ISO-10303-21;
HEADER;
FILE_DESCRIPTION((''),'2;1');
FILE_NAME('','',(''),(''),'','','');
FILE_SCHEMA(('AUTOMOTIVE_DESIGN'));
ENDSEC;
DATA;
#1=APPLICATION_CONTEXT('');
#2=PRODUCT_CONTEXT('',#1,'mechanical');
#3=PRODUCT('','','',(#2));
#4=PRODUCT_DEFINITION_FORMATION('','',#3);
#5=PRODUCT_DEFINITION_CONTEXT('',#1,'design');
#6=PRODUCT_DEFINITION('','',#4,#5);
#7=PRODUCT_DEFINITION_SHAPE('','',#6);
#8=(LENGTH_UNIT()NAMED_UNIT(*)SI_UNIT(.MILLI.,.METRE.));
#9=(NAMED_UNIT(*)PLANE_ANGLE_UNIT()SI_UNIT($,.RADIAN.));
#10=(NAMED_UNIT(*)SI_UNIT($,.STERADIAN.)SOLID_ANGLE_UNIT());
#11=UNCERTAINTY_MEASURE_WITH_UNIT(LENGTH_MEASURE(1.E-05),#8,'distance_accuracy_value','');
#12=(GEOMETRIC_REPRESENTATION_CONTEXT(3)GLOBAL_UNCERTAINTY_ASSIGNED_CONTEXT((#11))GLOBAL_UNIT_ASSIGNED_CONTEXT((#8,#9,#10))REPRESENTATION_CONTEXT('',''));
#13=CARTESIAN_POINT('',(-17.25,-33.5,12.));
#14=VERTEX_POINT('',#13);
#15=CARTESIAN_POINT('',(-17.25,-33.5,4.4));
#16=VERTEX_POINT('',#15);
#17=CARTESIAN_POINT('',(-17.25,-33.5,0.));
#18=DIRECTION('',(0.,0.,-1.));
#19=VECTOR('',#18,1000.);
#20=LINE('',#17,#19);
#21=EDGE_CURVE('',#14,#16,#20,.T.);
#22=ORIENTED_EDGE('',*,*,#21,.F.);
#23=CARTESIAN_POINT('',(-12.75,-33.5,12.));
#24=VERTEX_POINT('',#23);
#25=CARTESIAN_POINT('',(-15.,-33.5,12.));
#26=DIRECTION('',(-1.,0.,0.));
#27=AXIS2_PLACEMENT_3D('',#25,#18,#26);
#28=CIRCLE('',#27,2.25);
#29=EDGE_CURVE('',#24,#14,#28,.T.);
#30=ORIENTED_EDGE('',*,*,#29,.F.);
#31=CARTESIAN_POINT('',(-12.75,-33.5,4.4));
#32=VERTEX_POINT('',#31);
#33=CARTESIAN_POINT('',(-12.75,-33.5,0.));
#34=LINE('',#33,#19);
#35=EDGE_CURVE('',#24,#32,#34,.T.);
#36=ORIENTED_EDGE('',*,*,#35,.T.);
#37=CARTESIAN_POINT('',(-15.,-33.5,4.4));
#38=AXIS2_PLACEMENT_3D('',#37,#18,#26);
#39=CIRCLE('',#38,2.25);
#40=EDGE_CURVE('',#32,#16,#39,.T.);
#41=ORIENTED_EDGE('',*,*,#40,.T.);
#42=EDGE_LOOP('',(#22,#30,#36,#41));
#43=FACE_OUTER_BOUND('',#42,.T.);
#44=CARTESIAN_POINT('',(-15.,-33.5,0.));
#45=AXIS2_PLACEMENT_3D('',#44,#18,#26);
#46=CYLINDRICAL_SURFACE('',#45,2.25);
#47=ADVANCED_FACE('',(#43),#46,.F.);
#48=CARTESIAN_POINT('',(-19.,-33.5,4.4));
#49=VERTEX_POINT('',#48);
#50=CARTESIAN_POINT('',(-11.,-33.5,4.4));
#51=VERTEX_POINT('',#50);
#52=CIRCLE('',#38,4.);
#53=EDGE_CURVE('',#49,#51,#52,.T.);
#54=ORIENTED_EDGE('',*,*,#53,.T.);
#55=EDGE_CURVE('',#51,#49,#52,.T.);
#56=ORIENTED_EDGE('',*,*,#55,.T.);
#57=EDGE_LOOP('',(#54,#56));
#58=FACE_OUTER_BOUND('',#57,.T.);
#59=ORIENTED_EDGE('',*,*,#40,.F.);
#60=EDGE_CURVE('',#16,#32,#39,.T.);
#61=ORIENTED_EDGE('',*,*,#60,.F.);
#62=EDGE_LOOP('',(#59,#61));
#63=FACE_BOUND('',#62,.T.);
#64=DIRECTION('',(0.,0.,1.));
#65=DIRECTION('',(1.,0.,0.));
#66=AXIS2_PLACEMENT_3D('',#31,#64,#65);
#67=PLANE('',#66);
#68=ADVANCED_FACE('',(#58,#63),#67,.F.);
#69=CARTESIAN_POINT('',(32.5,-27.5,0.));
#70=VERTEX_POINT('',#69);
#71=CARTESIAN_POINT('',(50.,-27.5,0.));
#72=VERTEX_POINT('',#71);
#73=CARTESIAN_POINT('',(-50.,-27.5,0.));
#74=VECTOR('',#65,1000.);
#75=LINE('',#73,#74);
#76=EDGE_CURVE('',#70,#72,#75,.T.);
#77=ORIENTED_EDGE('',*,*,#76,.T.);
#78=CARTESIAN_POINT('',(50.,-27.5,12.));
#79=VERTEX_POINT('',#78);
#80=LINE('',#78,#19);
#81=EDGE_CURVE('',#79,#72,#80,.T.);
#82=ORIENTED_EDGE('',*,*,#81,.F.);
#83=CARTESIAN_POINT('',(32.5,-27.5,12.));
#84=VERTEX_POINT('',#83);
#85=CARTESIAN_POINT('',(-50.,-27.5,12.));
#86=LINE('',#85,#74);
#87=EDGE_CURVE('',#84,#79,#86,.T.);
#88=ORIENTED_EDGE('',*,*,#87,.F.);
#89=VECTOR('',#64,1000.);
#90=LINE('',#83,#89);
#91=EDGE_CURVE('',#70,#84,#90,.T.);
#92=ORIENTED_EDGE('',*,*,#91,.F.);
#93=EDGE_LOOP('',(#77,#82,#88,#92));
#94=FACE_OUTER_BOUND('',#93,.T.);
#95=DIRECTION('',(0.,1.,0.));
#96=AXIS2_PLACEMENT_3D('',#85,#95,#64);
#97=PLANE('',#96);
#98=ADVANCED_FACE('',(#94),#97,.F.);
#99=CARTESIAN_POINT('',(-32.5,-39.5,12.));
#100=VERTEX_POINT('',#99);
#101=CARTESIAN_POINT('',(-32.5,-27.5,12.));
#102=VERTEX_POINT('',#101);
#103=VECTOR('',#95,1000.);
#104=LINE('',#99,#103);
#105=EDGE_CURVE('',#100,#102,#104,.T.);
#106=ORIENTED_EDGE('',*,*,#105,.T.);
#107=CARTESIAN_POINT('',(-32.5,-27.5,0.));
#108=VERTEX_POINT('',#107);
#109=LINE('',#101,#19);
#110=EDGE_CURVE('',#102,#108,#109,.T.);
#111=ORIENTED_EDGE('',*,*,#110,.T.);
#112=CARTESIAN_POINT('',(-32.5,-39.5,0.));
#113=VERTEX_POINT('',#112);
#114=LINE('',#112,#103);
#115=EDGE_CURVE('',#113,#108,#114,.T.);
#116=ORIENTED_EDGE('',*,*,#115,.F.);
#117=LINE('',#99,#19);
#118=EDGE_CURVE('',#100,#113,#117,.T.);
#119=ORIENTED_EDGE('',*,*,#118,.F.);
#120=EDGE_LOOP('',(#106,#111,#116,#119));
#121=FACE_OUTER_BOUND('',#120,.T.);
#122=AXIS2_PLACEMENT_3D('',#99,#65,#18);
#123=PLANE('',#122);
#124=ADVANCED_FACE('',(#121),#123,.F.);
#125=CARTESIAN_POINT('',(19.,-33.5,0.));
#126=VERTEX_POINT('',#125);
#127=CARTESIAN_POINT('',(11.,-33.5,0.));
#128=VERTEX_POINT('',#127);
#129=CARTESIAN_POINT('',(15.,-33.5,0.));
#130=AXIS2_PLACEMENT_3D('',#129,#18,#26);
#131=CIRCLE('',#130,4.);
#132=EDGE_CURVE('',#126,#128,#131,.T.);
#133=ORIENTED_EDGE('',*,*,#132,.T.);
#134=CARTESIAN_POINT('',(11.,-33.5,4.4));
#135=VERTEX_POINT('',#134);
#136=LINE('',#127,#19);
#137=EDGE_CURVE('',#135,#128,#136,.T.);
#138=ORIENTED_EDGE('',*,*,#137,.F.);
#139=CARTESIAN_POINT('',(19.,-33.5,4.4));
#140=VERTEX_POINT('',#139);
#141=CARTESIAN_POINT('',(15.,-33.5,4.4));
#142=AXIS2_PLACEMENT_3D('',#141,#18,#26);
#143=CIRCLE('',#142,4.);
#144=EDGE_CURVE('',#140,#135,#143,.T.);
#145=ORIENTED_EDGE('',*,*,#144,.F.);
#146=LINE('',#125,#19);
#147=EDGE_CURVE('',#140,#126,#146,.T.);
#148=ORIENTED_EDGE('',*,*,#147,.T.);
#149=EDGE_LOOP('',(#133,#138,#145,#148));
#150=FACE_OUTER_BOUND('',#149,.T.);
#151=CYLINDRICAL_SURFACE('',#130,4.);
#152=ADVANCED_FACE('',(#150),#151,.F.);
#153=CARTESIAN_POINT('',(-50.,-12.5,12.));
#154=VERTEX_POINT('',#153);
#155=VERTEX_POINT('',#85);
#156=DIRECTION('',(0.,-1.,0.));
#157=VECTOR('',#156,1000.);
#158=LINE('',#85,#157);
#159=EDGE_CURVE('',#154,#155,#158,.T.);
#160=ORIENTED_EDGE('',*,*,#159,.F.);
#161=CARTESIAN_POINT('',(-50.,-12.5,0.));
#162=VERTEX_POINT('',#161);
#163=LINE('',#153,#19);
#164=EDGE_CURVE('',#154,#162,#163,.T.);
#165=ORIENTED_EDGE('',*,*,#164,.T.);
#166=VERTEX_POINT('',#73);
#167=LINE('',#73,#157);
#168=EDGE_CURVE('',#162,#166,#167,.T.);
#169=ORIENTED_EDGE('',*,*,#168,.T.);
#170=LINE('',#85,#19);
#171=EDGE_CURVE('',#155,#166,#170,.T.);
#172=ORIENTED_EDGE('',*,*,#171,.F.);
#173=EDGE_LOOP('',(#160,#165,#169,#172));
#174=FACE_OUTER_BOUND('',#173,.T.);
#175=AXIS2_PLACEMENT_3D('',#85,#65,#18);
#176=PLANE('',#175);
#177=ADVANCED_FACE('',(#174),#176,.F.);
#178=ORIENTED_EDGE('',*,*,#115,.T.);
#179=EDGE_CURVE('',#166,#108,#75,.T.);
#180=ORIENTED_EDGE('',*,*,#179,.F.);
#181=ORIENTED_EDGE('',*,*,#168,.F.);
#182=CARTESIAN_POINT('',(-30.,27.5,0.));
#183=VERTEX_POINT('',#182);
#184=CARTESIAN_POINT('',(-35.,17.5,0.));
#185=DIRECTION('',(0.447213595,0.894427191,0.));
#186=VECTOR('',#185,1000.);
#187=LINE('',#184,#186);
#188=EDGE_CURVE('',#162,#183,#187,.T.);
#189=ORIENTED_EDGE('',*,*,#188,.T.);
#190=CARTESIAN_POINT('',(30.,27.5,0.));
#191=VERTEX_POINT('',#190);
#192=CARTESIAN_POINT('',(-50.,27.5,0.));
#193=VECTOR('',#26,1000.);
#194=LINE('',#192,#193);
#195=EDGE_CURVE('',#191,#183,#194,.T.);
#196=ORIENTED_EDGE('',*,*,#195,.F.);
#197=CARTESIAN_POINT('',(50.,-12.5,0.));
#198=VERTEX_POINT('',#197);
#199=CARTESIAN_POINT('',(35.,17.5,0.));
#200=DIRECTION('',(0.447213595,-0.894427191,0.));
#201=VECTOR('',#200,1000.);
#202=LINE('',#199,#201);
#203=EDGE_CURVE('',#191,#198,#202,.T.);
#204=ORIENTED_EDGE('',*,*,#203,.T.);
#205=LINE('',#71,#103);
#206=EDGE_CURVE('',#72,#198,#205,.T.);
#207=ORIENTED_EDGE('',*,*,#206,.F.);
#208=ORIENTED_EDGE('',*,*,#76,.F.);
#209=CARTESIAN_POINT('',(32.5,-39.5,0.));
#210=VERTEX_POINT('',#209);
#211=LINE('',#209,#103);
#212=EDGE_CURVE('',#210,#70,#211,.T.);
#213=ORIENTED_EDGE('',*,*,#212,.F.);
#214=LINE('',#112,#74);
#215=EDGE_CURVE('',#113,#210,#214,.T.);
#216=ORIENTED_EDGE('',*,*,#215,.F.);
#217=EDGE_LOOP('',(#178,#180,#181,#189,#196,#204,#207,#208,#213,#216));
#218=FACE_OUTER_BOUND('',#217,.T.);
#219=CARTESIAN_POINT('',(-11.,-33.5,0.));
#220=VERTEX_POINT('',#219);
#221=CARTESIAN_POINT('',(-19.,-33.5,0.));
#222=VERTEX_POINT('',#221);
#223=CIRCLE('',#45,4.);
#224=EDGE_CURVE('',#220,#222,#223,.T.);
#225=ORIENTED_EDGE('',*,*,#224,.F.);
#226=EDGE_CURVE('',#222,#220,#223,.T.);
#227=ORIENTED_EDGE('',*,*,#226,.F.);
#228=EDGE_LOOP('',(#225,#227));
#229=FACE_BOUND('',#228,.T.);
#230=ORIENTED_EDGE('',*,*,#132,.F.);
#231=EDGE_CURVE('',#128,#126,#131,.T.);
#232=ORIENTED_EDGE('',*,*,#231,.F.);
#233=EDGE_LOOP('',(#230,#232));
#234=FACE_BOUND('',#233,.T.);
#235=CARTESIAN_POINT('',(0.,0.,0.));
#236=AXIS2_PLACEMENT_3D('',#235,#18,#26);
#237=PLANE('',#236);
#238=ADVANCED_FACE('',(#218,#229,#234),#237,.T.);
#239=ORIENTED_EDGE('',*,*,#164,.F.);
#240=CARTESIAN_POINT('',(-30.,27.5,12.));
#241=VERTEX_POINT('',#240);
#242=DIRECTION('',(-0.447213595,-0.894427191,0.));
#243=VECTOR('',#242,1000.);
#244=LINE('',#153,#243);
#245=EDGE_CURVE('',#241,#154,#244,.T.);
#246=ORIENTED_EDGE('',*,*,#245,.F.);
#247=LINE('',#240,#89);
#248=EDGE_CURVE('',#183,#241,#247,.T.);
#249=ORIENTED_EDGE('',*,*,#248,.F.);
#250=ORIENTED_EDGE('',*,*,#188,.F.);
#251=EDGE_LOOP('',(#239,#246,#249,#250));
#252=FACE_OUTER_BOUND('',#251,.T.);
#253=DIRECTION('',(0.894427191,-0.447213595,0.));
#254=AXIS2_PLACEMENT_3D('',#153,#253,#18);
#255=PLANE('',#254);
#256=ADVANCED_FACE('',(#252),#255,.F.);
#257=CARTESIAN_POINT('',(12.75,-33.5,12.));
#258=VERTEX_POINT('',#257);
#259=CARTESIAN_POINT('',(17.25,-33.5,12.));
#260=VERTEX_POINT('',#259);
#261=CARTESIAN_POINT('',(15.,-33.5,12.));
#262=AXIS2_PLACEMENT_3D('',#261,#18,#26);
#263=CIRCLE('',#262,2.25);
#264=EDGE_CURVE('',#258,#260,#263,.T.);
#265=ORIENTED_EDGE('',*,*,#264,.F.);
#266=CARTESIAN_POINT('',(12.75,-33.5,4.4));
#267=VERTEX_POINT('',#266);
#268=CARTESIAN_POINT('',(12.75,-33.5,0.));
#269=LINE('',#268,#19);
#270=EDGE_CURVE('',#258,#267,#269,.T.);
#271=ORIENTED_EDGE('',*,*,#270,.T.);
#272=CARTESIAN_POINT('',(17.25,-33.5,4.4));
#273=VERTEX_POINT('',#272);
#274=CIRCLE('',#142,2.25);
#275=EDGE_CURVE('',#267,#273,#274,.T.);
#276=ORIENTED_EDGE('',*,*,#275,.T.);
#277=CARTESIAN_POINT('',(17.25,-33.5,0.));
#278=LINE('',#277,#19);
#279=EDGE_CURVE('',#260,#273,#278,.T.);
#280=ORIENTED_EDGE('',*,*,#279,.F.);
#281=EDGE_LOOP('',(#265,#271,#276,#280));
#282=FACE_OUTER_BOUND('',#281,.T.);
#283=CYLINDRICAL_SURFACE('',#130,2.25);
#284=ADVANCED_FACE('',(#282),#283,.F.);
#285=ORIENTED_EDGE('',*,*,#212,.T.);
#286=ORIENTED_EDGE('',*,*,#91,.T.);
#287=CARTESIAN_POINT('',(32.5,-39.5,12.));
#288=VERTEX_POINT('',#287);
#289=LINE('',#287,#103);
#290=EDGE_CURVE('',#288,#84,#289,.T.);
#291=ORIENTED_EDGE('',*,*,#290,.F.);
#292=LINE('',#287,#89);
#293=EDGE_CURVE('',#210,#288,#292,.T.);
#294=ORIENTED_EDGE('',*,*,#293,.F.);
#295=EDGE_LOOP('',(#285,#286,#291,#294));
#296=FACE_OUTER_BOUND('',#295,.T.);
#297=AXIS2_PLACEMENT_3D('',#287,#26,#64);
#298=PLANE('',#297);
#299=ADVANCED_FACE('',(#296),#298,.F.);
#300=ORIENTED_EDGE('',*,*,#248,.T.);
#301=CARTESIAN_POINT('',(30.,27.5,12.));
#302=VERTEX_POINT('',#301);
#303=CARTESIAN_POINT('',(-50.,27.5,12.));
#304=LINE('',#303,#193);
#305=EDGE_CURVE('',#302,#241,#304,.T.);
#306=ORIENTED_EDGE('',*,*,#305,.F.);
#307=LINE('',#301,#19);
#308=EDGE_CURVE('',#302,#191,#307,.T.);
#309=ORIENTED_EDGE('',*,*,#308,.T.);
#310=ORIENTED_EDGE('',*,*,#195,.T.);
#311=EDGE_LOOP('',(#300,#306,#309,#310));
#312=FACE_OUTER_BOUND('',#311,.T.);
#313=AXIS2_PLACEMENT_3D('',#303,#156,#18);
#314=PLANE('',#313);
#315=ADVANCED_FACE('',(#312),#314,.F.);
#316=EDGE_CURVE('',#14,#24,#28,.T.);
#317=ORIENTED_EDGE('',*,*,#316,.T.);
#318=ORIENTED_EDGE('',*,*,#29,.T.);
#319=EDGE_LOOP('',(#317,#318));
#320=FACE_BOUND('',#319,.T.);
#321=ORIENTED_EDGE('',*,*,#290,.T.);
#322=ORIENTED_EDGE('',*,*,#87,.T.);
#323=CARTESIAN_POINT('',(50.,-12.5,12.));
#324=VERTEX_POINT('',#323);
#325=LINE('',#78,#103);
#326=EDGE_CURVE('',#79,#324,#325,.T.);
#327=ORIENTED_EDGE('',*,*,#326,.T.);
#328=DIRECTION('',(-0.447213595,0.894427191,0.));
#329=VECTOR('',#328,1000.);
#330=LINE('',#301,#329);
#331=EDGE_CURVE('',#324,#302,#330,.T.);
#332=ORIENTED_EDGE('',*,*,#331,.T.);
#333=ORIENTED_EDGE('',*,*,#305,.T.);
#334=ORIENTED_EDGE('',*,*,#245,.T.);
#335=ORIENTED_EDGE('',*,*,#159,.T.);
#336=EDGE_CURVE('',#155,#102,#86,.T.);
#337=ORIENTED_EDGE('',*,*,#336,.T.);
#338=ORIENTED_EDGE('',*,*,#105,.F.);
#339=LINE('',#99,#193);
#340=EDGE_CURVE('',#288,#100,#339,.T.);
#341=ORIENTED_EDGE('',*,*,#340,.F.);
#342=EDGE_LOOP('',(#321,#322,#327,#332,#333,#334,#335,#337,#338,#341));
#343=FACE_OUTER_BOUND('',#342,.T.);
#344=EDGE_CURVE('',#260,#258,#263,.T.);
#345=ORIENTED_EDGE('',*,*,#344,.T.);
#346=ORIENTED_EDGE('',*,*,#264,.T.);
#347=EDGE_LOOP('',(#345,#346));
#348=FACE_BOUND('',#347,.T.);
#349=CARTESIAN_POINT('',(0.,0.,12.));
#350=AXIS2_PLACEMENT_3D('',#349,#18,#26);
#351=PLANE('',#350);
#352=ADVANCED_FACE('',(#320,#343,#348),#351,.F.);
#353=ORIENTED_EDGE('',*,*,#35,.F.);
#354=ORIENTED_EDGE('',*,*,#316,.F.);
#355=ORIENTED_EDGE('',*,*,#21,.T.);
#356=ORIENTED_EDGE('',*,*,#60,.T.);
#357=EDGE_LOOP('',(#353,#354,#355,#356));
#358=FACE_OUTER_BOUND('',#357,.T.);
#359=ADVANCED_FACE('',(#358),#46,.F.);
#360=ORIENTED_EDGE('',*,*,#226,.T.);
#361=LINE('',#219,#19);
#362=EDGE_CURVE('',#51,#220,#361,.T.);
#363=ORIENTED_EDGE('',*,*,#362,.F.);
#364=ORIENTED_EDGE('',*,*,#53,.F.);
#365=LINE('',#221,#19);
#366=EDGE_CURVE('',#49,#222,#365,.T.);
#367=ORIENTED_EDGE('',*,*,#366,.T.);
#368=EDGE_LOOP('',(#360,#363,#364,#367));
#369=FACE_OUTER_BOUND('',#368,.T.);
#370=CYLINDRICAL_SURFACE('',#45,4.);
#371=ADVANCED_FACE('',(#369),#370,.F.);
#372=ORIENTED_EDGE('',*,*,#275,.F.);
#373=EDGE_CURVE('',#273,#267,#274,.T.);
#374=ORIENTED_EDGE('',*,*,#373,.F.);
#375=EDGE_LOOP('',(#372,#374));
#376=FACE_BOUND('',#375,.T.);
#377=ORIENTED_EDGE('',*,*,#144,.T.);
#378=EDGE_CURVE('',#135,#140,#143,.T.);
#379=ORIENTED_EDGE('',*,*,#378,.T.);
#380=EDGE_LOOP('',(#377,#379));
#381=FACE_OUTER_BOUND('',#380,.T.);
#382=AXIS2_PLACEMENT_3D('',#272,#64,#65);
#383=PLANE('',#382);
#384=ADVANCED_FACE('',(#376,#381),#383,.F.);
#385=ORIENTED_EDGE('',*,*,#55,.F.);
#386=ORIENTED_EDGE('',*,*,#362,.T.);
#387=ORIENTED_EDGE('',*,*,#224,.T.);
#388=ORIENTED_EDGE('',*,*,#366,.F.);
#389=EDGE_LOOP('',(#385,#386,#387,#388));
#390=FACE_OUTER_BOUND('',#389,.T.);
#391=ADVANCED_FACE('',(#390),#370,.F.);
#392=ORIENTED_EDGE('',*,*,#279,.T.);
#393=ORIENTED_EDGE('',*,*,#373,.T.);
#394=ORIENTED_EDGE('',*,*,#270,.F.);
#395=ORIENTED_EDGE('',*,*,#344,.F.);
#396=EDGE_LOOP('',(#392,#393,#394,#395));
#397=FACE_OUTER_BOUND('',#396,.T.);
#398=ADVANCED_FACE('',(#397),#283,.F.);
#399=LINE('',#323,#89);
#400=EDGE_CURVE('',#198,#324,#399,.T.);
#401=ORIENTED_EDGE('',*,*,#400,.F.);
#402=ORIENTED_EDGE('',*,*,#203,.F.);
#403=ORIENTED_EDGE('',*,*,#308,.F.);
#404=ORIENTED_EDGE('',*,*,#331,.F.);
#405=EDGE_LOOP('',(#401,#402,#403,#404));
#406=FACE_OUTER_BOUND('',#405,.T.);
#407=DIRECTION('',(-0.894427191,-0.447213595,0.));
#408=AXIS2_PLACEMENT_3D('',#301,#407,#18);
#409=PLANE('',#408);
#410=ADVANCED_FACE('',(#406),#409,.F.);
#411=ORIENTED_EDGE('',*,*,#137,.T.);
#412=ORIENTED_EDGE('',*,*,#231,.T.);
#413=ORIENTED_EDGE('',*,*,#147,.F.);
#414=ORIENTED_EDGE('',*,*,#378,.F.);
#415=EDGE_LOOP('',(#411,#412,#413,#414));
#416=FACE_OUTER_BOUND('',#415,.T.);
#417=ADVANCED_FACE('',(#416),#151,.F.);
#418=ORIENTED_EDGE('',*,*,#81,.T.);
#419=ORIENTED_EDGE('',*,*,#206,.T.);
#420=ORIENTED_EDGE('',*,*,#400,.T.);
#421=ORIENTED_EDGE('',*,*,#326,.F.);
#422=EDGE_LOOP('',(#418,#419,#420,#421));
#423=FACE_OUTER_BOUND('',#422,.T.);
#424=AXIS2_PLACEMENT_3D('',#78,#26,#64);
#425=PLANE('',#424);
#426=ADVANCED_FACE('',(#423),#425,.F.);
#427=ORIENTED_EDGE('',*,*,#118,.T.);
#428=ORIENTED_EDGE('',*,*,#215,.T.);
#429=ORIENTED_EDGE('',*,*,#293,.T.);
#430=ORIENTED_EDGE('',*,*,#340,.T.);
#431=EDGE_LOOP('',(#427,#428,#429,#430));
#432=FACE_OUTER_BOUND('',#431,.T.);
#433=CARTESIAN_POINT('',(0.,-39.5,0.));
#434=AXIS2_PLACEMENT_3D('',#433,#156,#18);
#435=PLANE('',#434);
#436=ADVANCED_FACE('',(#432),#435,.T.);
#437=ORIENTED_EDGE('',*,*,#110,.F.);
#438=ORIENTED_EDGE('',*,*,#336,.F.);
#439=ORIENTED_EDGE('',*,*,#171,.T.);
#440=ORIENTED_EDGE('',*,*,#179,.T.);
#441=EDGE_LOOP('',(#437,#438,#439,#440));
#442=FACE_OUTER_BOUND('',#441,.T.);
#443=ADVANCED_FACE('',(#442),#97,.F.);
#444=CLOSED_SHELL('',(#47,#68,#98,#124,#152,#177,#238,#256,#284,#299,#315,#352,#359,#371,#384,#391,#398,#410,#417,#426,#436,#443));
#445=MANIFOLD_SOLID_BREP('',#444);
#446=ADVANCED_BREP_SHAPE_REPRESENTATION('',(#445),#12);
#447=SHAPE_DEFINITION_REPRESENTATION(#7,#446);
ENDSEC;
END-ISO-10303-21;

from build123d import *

# Parameters (mm, degrees)
SKETCH1_W                                           = 100
SKETCH1_H                                           = 55
BOSS_EXTRUDE1_DEPTH                                 = 12
SKETCH2_W                                           = 65
SKETCH2_H                                           = 12
BOSS_EXTRUDE2_DEPTH                                 = 12
CBORE_FOR_M4_HEX_SOCKET_HEAD_CAP_SCREW1_D           = 4.5
CBORE_FOR_M4_HEX_SOCKET_HEAD_CAP_SCREW1_CBORE_D     = 8
CBORE_FOR_M4_HEX_SOCKET_HEAD_CAP_SCREW1_CBORE_DEPTH = 4.4
CHAMFER1_SIZE                                       = 40
CHAMFER1_SIZE2                                      = 20
CHAMFER2_SIZE                                       = 20
CHAMFER2_SIZE2                                      = 40


with BuildPart() as part:
    # Sketch1 → Boss-Extrude1 (new body)
    with BuildSketch(Plane.XY):
        Rectangle(SKETCH1_W, SKETCH1_H)
    extrude(amount=BOSS_EXTRUDE1_DEPTH)

    # Sketch2 → Boss-Extrude2 (add)
    with BuildSketch(Plane.XZ.offset(27.5)):
        with Locations((0, 6)):
            Rectangle(SKETCH2_W, SKETCH2_H)
    extrude(amount=BOSS_EXTRUDE2_DEPTH)

    # CBORE for M4 Hex Socket Head Cap Screw1 (through all)
    with Locations(Plane(origin=(0, 0, 0), x_dir=(-1, 0, 0), z_dir=(0, 0, -1))):
        with Locations((15, -33.5), (-15, -33.5)):
            CounterBoreHole(CBORE_FOR_M4_HEX_SOCKET_HEAD_CAP_SCREW1_D / 2, CBORE_FOR_M4_HEX_SOCKET_HEAD_CAP_SCREW1_CBORE_D / 2, CBORE_FOR_M4_HEX_SOCKET_HEAD_CAP_SCREW1_CBORE_DEPTH)

    # Chamfer1
    chamfer1_edges = [part.edges().sort_by_distance(p)[0] for p in [
        (50, 27.5, 6),
    ]]
    chamfer1_side = [part.faces().sort_by_distance(p)[0] for p in [
        (50, 0, 6),
    ]]
    chamfer(chamfer1_edges, length=CHAMFER1_SIZE, length2=CHAMFER1_SIZE2, reference=chamfer1_side[0])

    # Chamfer2
    chamfer2_edges = [part.edges().sort_by_distance(p)[0] for p in [
        (-50, 27.5, 6),
    ]]
    chamfer2_side = [part.faces().sort_by_distance(p)[0] for p in [
        (-10, 27.5, 6),
    ]]
    chamfer(chamfer2_edges, length=CHAMFER2_SIZE, length2=CHAMFER2_SIZE2, reference=chamfer2_side[0])


solid = part.part
